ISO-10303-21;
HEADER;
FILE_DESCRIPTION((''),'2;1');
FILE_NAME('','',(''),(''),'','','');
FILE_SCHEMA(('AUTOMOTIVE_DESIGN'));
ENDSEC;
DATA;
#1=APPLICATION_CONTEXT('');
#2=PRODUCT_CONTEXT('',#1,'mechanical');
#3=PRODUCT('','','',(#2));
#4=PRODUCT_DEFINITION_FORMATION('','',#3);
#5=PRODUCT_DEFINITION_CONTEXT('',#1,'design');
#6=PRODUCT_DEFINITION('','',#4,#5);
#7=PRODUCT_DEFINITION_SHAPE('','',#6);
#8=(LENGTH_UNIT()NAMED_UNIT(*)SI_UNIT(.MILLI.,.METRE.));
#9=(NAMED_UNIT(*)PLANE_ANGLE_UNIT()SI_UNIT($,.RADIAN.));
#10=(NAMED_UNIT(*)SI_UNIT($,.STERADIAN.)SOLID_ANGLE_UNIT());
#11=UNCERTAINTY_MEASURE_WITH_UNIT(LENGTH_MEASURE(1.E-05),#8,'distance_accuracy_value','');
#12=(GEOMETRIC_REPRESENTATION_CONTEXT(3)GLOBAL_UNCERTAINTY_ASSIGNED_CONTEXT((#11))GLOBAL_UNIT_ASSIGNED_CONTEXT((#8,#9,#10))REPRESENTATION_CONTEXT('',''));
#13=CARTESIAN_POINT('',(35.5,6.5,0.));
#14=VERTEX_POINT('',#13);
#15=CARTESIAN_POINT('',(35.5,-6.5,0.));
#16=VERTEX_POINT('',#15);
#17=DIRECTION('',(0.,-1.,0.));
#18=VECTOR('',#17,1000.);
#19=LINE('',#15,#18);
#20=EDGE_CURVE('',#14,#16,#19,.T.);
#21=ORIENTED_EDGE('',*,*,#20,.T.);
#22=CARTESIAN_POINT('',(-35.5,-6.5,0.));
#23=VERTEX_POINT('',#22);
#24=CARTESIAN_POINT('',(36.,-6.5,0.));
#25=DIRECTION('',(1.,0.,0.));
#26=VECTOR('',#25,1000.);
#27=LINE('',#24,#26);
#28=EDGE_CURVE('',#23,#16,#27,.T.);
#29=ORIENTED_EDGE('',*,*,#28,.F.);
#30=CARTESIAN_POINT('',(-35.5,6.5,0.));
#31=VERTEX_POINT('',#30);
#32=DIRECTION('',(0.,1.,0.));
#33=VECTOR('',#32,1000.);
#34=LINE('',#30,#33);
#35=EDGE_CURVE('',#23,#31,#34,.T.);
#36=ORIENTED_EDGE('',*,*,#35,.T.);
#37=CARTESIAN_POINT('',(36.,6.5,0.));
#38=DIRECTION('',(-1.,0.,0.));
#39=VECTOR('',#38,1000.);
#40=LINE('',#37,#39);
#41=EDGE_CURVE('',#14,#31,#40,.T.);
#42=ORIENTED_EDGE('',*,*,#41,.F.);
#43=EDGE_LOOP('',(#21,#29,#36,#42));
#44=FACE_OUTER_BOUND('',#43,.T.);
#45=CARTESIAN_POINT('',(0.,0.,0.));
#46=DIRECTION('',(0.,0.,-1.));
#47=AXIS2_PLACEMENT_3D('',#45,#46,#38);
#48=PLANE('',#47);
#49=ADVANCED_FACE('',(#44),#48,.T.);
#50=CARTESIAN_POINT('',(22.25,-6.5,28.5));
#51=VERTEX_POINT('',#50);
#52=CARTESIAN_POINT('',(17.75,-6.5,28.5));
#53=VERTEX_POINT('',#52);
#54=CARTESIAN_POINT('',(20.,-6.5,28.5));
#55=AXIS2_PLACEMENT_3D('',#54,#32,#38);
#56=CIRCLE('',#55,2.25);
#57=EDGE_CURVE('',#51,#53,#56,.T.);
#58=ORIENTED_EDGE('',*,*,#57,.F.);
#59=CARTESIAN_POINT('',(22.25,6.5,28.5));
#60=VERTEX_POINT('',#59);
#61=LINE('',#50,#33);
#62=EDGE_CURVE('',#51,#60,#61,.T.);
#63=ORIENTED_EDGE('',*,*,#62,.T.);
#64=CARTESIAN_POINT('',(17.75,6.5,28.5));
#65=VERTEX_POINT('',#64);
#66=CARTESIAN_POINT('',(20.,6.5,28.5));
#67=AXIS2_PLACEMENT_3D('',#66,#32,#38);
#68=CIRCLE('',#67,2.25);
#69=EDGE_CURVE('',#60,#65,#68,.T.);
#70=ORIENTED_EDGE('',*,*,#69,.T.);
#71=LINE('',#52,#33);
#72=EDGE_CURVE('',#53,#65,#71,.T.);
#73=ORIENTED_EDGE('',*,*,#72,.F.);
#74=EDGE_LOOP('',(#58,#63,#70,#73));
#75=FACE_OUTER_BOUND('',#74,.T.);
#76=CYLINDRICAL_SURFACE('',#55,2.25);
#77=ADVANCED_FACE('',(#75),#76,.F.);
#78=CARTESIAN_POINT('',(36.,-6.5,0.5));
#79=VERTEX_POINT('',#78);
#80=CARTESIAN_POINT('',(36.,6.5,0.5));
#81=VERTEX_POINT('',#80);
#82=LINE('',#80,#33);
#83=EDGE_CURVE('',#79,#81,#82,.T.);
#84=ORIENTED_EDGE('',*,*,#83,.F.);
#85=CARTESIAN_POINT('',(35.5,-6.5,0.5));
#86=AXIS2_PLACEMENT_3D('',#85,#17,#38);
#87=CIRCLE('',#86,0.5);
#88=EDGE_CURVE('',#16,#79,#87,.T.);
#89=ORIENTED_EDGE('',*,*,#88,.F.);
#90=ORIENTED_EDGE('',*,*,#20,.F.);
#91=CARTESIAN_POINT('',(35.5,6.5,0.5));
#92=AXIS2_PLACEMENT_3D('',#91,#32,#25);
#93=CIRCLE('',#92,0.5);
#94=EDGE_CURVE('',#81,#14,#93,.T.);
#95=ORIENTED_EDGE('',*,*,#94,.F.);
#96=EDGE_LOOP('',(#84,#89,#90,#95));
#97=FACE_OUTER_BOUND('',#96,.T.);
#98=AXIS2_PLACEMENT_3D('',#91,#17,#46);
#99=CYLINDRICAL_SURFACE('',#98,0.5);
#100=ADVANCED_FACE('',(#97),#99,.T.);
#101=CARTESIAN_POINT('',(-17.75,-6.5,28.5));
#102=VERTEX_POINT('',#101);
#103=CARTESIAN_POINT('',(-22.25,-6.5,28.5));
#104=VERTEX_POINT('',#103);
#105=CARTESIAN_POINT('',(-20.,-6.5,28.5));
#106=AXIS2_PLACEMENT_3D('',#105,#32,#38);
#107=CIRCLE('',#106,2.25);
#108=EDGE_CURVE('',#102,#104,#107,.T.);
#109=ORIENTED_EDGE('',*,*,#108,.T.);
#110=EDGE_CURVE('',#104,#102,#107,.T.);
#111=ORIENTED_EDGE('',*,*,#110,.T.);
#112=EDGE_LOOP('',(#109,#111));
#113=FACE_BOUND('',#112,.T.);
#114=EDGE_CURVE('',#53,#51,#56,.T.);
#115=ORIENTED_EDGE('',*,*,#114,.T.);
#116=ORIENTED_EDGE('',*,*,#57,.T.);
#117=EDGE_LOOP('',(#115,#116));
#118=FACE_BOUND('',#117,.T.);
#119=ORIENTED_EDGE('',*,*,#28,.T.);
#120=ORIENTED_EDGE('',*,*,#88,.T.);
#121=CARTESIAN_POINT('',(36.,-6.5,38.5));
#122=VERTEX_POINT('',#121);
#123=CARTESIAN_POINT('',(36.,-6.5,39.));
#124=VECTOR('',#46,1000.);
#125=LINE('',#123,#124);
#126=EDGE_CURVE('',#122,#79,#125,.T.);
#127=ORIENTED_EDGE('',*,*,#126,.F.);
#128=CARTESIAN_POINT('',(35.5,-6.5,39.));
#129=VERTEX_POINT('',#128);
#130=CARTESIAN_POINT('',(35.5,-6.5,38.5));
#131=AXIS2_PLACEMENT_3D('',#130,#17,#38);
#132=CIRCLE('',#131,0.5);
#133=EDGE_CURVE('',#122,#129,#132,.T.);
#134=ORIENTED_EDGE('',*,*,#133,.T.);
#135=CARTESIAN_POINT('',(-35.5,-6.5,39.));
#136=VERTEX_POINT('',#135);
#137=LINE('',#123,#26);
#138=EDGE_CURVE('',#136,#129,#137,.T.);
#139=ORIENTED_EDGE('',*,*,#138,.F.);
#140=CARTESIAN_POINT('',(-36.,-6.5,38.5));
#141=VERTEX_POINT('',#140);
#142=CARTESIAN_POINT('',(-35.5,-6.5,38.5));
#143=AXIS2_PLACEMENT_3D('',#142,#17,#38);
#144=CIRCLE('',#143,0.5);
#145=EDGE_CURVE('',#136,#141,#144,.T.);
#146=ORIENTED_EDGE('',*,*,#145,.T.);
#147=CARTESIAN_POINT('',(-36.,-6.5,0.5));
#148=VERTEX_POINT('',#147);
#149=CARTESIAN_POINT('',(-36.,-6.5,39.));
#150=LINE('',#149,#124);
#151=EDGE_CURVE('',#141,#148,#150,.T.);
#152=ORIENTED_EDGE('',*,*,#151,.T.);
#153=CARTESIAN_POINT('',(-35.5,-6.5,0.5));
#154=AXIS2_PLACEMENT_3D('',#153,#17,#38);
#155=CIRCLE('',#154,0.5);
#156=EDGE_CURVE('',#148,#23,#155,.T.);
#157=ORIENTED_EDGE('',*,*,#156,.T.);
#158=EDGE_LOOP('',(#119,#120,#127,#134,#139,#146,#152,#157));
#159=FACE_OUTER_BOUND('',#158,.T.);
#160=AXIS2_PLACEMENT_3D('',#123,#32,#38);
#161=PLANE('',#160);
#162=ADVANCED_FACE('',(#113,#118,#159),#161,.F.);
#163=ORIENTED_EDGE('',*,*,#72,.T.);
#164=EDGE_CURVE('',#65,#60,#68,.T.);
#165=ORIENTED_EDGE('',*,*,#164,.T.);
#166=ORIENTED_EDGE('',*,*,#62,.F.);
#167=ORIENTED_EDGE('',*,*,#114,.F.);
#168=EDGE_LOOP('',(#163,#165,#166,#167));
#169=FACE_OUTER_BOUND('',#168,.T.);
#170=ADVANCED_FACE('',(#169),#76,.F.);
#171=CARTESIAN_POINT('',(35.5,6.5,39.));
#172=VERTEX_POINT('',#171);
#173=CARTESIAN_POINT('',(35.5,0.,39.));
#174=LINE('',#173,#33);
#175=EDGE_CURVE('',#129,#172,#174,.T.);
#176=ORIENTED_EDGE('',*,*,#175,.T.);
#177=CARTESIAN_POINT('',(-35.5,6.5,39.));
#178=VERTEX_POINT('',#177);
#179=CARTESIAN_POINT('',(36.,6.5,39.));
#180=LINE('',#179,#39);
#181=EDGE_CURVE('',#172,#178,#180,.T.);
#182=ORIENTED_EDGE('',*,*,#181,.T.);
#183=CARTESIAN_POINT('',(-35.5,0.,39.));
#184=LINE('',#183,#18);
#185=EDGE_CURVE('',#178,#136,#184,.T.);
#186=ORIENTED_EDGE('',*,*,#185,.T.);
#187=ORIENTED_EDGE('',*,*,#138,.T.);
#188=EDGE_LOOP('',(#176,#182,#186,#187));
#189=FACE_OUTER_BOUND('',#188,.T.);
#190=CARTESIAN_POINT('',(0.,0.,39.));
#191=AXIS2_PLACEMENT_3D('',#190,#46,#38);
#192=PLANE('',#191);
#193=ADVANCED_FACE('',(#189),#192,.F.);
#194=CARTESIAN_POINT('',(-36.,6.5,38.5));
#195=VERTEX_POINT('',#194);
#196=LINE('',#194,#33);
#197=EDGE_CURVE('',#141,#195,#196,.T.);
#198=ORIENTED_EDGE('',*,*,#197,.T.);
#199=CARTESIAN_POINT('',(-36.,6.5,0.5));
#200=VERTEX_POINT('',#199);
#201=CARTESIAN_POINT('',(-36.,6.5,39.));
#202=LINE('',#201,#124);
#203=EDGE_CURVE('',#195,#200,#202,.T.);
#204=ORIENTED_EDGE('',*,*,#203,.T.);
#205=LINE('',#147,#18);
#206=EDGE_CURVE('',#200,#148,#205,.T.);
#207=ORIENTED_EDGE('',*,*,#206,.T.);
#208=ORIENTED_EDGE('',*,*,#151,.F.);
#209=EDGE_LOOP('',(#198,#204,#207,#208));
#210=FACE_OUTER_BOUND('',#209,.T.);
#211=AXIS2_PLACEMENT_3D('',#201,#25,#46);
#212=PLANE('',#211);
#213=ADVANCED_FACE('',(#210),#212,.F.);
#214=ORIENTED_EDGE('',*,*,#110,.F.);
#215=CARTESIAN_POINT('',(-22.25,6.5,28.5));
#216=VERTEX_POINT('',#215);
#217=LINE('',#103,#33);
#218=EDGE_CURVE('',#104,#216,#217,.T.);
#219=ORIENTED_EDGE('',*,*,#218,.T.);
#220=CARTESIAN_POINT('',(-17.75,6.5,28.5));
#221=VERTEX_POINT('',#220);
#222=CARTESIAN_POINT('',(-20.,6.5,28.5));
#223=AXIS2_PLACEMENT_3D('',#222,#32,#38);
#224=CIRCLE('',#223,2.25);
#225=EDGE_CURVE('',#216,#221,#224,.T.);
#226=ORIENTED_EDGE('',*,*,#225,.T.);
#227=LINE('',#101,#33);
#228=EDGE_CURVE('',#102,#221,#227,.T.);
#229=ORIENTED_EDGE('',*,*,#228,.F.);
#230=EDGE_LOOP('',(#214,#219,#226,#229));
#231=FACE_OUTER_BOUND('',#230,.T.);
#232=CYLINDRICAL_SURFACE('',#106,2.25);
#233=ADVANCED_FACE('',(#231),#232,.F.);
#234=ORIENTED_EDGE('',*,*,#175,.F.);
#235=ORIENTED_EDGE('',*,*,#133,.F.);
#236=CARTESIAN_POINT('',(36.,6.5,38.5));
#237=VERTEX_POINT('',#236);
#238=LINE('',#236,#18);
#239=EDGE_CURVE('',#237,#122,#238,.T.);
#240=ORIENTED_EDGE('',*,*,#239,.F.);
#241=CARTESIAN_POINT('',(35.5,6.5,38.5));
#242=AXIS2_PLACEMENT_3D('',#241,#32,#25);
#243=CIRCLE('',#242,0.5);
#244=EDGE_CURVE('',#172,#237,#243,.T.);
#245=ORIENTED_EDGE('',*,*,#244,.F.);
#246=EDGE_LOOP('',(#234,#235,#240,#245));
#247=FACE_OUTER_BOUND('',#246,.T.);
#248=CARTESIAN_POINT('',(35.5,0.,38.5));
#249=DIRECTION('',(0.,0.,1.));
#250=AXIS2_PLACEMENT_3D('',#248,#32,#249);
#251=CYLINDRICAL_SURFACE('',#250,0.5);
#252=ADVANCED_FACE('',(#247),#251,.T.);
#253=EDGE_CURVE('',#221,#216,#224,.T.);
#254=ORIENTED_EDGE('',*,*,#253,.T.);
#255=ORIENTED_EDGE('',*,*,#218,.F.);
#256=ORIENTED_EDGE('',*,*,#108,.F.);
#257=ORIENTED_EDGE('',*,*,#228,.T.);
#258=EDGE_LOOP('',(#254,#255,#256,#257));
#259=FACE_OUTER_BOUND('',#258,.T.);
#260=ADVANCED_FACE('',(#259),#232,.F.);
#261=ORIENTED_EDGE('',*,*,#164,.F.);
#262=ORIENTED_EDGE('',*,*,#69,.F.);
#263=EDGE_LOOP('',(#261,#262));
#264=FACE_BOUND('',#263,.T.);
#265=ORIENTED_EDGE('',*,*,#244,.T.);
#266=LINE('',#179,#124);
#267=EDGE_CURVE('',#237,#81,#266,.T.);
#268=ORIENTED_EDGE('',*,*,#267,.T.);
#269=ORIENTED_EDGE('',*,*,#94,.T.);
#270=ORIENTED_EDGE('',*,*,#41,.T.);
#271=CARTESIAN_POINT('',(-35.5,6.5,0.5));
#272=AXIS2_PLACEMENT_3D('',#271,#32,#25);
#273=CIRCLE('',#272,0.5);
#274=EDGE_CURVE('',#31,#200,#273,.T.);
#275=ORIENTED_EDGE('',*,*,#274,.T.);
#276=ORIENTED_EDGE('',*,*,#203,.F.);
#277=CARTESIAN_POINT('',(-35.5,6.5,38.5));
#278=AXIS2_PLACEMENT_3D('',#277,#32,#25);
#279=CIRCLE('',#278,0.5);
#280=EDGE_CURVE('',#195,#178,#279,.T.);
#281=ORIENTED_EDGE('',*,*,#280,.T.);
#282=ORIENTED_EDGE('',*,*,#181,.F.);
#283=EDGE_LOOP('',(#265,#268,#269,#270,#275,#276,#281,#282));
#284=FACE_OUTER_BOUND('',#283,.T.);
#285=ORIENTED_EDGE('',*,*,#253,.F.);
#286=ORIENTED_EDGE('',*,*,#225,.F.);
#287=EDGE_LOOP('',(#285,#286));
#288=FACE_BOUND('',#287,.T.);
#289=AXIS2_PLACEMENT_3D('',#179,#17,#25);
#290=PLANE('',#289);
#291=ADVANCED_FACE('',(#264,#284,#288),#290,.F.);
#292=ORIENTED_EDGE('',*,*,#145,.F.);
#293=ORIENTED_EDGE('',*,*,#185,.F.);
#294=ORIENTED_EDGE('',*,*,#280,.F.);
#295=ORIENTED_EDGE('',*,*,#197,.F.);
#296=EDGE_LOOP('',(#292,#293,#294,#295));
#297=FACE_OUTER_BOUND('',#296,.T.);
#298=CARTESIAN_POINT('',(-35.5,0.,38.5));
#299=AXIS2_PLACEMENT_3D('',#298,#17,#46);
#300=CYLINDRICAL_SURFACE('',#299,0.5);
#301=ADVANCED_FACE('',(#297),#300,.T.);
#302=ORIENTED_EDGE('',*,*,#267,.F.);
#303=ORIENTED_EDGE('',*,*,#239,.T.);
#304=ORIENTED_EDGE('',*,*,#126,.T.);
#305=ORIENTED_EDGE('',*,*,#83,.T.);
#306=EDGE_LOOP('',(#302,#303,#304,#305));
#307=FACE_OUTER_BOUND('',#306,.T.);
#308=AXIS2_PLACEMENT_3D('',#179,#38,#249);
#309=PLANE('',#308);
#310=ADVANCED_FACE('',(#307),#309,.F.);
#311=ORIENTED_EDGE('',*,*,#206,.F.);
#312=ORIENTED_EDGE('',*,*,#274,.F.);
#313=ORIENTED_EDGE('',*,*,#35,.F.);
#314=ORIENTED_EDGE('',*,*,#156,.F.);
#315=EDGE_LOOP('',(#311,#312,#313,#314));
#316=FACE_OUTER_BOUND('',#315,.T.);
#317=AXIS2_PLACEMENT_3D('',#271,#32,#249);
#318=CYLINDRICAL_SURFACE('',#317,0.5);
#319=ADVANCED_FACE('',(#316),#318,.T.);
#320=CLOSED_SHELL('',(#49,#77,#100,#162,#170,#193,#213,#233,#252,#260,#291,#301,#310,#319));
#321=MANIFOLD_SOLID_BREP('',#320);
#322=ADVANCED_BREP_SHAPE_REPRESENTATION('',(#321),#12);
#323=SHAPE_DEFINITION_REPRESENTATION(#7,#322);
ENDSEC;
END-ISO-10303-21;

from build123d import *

# Parameters (mm, degrees)
SKETCH_1_W          = 72
SKETCH_1_H          = 13
EXTRUDE_1_DEPTH     = 39
FILLET_1_R          = 0.5
SKETCH_2_R          = 2.25
CUT_EXTRUDE_1_DEPTH = 55.644304369


with BuildPart() as part:
    # 草图1 → 凸台-拉伸1 (new body)
    with BuildSketch(Plane.XY):
        Rectangle(SKETCH_1_W, SKETCH_1_H)
    extrude(amount=EXTRUDE_1_DEPTH)

    # 圆角1
    fillet_1_edges = [part.edges().sort_by_distance(p)[0] for p in [
        (36, 0, 39),
        (-36, 0, 39),
        (36, 0, 0),
        (-36, 0, 0),
    ]]
    fillet(fillet_1_edges, radius=FILLET_1_R)

    # 草图2 → 切除-拉伸1 (cut, through all)
    with BuildSketch(Plane(origin=(0, 6.5, 0), x_dir=(1, 0, 0), z_dir=(0, 1, 0))):
        with Locations(Location((-20, -28.5, 0), (0, 0, 180))):
            Circle(SKETCH_2_R)
        with Locations(Location((20, -28.5, 0), (0, 0, 180))):
            Circle(SKETCH_2_R)
    extrude(amount=-CUT_EXTRUDE_1_DEPTH, mode=Mode.SUBTRACT)


solid = part.part
